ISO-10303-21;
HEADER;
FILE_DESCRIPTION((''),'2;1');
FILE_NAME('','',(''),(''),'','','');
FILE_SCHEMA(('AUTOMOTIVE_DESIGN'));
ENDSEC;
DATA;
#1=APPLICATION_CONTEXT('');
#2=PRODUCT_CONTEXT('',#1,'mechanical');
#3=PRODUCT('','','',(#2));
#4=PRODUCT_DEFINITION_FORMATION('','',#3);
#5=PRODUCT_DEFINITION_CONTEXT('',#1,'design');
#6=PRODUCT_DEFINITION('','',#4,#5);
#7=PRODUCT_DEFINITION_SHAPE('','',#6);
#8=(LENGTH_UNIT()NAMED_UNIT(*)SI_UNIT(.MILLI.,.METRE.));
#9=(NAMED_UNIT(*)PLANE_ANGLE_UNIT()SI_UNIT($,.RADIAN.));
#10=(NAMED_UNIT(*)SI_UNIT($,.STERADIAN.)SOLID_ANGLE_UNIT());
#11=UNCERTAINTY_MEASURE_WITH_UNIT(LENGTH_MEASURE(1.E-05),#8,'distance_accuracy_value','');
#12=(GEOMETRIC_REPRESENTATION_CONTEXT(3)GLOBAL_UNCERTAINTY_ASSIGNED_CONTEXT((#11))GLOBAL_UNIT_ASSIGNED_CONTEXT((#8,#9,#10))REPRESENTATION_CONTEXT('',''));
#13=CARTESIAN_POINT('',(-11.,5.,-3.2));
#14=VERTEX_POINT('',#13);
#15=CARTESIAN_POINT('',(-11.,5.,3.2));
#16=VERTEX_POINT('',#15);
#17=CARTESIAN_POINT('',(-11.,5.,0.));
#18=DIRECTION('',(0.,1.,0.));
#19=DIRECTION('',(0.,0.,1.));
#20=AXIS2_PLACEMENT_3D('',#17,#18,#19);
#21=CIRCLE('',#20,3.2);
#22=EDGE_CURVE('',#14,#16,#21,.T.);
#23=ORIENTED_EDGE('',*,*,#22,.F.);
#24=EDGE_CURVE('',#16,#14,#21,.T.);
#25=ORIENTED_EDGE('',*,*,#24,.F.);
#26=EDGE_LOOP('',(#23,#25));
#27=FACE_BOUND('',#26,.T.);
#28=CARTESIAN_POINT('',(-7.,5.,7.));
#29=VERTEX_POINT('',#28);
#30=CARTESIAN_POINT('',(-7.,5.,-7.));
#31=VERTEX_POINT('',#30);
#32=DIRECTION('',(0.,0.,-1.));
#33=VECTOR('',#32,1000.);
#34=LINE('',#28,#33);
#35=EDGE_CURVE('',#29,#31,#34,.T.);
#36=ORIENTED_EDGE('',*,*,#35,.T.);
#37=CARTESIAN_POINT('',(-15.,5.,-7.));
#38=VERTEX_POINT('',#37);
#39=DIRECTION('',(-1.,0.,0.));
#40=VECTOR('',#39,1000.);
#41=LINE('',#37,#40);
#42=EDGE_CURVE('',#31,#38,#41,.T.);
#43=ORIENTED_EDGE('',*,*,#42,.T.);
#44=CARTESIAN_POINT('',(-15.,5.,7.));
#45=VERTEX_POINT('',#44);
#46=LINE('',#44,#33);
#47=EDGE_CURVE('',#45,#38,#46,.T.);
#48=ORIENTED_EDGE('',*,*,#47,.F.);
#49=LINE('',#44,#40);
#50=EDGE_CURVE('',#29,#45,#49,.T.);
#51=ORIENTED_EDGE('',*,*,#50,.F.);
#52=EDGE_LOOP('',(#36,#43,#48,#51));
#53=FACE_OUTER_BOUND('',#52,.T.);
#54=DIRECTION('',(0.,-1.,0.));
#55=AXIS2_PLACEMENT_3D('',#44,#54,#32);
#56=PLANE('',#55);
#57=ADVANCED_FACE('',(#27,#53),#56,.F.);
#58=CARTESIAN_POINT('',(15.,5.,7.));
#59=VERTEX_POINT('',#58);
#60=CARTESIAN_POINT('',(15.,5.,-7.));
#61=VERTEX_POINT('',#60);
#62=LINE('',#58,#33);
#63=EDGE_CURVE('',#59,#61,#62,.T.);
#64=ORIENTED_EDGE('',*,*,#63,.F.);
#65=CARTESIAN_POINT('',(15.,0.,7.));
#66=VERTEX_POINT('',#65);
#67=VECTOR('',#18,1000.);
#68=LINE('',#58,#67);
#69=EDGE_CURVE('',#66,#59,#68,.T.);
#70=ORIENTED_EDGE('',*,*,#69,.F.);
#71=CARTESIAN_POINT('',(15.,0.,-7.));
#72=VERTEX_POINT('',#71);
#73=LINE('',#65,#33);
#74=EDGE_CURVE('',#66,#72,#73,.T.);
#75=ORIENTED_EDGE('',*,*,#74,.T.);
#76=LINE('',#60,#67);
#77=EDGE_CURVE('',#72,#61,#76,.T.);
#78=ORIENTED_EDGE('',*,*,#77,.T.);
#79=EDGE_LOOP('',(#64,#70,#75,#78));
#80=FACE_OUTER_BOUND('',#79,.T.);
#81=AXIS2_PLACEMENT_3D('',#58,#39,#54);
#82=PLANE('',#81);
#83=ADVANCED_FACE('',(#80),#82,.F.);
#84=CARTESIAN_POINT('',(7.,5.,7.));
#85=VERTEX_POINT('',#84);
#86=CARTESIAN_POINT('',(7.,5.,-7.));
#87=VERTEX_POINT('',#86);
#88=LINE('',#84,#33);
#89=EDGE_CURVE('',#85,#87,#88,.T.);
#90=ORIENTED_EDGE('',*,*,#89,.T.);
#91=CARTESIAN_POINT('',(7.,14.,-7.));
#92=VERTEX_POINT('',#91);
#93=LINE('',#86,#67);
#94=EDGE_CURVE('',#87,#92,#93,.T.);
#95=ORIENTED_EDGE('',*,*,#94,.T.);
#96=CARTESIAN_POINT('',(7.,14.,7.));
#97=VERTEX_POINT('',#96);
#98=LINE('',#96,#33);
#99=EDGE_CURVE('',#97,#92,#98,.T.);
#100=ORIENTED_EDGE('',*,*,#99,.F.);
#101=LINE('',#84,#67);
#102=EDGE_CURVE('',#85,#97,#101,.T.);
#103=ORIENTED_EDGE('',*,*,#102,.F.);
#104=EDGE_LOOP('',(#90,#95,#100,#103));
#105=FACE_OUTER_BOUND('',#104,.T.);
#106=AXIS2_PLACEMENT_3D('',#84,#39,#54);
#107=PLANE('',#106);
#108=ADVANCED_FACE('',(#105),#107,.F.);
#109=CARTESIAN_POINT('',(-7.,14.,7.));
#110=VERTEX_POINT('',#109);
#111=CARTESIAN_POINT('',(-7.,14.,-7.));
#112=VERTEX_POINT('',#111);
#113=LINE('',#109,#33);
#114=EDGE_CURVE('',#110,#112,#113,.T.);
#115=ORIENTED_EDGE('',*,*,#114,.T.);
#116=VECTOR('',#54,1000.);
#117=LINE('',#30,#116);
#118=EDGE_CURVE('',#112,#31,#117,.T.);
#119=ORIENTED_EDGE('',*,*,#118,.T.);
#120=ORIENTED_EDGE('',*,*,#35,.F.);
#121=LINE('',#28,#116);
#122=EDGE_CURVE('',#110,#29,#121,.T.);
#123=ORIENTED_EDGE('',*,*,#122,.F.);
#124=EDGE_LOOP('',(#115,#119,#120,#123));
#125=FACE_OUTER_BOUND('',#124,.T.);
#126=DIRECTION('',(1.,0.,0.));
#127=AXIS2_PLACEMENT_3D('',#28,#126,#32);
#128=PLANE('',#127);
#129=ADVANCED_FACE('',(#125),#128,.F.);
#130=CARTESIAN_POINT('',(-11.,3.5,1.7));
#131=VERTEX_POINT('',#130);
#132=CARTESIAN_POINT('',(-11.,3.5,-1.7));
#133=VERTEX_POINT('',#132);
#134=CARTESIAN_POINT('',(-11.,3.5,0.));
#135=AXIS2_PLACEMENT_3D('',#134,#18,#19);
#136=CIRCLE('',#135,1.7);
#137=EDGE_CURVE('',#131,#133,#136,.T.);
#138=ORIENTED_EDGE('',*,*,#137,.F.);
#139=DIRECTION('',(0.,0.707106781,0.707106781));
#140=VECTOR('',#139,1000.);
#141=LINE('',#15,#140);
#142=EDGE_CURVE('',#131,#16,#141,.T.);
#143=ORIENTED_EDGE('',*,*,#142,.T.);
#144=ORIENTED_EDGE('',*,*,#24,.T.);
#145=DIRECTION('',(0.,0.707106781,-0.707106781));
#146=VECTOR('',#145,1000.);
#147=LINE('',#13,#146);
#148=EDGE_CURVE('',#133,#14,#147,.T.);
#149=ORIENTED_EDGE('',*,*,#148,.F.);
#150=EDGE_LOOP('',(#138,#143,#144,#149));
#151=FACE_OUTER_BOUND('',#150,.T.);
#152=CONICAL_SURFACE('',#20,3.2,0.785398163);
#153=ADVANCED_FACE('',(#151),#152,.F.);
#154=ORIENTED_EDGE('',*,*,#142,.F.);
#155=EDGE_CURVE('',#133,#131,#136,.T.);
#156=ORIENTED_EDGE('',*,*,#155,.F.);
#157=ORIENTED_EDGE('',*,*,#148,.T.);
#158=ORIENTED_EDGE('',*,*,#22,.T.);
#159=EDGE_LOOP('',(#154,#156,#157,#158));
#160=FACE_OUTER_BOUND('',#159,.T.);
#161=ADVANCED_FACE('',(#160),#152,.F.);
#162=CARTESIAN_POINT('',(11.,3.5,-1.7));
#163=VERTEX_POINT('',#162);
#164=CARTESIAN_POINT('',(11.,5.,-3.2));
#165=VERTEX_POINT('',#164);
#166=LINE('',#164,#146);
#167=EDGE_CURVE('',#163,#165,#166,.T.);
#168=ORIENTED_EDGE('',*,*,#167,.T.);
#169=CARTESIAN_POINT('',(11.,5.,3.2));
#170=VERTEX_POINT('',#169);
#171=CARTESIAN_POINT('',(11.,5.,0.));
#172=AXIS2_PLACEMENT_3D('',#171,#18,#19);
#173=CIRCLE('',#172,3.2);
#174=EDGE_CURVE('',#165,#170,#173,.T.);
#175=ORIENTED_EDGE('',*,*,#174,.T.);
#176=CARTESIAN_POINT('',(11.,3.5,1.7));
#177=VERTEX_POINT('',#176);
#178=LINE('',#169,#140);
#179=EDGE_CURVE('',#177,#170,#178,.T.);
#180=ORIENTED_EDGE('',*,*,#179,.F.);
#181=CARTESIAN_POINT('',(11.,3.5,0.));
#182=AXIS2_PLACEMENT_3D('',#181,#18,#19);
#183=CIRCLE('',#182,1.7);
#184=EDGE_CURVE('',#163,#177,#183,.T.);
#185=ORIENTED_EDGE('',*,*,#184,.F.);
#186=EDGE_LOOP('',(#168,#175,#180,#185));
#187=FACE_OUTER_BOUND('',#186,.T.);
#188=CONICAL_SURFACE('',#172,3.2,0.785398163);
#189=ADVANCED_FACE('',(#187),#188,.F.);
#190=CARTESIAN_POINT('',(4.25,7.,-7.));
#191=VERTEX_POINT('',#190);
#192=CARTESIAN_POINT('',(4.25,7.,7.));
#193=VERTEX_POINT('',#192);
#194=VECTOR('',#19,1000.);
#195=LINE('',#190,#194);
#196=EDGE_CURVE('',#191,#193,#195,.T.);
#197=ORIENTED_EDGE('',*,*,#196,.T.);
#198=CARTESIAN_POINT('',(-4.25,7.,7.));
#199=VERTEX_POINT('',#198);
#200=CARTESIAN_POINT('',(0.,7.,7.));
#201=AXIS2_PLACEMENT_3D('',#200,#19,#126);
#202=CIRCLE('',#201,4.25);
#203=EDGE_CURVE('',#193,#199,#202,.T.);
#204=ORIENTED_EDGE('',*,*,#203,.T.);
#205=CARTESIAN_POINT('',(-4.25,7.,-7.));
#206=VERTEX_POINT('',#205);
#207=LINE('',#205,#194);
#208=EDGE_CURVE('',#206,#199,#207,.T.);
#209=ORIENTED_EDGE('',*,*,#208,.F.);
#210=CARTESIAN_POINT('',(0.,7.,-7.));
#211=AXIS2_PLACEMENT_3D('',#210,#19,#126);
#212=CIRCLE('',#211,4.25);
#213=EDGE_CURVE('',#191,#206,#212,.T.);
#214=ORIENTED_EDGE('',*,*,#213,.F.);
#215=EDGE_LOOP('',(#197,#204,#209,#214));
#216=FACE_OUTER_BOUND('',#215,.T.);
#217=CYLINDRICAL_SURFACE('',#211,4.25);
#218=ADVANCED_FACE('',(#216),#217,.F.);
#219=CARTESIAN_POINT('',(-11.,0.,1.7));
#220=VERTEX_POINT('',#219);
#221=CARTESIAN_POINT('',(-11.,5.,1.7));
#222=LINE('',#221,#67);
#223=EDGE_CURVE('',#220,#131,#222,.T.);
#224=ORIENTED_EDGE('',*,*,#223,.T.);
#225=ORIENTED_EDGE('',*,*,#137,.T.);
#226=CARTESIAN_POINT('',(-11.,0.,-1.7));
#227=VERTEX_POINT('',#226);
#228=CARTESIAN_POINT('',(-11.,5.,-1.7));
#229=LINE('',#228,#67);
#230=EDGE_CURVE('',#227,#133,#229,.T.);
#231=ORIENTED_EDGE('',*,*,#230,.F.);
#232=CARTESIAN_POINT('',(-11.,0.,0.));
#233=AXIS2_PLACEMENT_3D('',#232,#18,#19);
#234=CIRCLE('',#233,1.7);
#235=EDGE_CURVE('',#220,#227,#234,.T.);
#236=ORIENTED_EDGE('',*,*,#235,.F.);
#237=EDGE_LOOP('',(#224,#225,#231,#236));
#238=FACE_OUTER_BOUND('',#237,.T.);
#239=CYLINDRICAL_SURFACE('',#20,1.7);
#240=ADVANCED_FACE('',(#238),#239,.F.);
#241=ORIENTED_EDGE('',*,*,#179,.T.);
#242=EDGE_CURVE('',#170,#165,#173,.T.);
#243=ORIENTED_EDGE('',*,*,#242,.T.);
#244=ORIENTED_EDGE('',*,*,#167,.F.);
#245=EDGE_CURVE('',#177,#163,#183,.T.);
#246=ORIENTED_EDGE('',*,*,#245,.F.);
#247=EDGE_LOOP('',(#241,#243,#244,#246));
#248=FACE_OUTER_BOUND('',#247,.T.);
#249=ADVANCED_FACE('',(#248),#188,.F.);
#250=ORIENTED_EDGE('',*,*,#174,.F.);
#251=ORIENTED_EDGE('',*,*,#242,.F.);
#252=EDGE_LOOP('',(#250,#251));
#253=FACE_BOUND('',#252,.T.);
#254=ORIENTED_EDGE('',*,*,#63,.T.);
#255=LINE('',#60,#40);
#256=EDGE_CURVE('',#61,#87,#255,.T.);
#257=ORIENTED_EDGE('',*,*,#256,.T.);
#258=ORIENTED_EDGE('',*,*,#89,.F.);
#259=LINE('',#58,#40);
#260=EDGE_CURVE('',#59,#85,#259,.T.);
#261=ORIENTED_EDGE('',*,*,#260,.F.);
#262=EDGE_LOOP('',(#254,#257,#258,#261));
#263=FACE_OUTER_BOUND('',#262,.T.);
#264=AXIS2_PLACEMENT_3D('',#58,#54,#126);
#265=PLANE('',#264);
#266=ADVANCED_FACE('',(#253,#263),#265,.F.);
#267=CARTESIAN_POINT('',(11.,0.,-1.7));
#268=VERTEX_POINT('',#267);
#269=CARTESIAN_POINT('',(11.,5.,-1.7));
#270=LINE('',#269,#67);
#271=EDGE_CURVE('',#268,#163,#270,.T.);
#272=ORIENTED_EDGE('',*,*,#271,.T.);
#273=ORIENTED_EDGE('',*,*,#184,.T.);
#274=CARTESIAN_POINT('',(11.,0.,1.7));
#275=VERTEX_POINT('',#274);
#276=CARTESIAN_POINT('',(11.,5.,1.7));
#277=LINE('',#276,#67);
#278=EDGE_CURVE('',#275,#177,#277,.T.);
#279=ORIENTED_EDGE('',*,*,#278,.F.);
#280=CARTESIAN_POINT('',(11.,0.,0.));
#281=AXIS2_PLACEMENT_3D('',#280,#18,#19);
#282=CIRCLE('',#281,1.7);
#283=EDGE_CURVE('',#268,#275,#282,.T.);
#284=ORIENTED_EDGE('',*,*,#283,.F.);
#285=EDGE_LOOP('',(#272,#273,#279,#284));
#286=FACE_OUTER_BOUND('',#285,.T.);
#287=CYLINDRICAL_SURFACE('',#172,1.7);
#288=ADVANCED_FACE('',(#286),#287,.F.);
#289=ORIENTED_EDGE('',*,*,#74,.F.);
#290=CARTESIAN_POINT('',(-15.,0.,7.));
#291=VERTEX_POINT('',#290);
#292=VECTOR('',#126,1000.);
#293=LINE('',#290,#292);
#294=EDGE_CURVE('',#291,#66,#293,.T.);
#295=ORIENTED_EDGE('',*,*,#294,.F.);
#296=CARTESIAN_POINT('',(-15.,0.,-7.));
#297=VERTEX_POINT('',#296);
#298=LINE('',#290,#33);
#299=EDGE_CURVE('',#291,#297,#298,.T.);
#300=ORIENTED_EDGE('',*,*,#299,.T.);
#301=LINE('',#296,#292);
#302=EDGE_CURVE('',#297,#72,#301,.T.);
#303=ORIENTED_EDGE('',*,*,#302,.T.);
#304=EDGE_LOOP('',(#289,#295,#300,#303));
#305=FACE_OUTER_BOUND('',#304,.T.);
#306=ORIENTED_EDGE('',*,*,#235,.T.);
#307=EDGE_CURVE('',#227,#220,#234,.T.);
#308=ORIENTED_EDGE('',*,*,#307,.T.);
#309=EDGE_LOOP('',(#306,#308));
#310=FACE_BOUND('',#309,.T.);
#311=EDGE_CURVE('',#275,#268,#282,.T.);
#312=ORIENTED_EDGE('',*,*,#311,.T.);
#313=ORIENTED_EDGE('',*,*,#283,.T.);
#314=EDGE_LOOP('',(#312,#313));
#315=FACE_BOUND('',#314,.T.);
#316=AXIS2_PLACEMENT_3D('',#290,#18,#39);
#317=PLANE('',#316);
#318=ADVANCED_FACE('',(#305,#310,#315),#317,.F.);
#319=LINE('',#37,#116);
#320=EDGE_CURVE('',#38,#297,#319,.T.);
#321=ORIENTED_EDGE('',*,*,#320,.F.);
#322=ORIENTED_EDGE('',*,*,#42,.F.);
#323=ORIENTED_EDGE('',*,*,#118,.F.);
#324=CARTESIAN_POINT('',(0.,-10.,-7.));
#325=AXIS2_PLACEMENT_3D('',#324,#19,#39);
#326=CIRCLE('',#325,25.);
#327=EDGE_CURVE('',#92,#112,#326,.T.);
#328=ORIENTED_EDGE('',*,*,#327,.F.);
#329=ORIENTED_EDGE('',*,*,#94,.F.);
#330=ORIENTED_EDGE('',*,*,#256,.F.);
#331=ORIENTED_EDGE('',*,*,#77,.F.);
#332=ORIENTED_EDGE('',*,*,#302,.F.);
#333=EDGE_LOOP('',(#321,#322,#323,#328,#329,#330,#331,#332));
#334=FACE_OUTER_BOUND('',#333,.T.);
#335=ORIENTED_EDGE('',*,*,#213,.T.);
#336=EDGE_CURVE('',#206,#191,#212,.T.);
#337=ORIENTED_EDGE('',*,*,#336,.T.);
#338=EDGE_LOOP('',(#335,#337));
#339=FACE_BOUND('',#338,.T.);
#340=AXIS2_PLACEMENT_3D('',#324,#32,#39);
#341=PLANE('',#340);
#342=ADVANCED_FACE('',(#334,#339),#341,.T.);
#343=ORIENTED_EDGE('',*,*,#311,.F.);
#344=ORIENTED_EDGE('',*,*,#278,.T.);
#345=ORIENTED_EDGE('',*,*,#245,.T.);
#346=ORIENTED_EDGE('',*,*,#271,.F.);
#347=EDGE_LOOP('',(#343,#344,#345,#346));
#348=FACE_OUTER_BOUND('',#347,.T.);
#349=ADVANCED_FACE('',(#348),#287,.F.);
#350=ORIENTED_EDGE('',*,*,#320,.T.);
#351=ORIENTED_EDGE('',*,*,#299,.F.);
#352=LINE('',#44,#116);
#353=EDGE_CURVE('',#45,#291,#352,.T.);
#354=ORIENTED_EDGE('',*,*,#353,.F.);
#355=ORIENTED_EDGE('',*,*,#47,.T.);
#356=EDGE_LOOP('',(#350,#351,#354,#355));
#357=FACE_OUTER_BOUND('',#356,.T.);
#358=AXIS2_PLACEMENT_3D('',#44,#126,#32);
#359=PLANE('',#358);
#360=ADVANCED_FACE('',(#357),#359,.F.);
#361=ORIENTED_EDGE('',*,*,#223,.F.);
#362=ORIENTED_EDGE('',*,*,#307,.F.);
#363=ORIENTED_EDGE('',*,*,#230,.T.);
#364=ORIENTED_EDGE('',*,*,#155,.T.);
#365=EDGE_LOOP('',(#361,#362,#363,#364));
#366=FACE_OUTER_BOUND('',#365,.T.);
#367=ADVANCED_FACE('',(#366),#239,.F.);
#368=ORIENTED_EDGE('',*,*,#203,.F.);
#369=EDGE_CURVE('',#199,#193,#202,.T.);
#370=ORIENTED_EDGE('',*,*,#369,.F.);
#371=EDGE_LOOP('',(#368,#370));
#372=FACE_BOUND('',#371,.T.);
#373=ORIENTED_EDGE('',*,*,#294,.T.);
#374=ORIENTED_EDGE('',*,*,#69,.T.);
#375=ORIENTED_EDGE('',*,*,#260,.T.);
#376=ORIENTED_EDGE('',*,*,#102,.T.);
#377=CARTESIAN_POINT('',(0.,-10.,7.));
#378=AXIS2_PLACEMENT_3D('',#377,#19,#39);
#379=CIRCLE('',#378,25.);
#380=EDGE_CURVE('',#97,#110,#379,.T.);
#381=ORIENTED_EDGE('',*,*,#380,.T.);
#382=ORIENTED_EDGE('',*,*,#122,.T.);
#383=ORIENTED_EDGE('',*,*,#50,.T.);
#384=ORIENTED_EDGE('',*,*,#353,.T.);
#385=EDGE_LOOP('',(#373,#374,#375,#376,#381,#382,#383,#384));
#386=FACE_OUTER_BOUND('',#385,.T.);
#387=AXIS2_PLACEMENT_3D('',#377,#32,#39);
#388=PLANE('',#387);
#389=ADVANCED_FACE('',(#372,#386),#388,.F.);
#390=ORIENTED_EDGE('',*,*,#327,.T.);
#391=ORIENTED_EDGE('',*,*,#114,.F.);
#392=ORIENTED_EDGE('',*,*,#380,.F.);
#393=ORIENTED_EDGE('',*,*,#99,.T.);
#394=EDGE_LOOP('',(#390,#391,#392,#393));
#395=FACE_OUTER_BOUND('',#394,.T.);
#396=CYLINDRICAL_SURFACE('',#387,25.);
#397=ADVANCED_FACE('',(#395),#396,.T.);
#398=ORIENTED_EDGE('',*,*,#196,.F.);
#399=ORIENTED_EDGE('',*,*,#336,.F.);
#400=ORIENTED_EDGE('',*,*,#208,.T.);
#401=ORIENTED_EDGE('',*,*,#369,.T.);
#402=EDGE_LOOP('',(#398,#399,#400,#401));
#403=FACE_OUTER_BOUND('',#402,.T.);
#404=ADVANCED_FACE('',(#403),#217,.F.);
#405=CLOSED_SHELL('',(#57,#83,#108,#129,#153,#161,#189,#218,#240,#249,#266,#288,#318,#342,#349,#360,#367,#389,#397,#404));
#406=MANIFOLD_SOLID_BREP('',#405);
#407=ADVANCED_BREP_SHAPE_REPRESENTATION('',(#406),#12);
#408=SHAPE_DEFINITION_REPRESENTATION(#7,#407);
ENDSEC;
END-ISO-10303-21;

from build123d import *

# Parameters (mm, degrees)
EXTRUDE_1_DEPTH           = 7
HOLE_WIZARD_1_D           = 3.4
HOLE_WIZARD_1_CSINK_D     = 6.4
HOLE_WIZARD_1_CSINK_ANGLE = 90
SKETCH_5_R                = 4.25
CUT_EXTRUDE_1_DEPTH       = 26.416530054


with BuildPart() as part:
    # 草图1 → 凸台-拉伸1 (new, symmetric)
    with BuildSketch(Plane.XY):
        with BuildLine():
            Line((-15, 5), (-7, 5))
            Line((-7, 5), (-7, 14))
            ThreePointArc((-7, 14), (0, 15), (7, 14))
            Line((7, 14), (7, 5))
            Line((7, 5), (15, 5))
            Line((15, 5), (15, 0))
            Line((15, 0), (-15, 0))
            Line((-15, 0), (-15, 5))
        make_face()
    extrude(amount=EXTRUDE_1_DEPTH, both=True)

    # 打孔尺寸开槽半沉头螺钉的类型1 (through all)
    with Locations(Plane(origin=(0, 5, 0), x_dir=(1, 0, 0), z_dir=(0, 1, 0))):
        with Locations((-11, 0), (11, 0)):
            CounterSinkHole(HOLE_WIZARD_1_D / 2, HOLE_WIZARD_1_CSINK_D / 2, counter_sink_angle=HOLE_WIZARD_1_CSINK_ANGLE)

    # 草图5 → 切除-拉伸1 (cut, through all)
    with BuildSketch(Plane.XY.offset(7)):
        with Locations((0, 7)):
            Circle(SKETCH_5_R)
    extrude(amount=-CUT_EXTRUDE_1_DEPTH, mode=Mode.SUBTRACT)


solid = part.part
